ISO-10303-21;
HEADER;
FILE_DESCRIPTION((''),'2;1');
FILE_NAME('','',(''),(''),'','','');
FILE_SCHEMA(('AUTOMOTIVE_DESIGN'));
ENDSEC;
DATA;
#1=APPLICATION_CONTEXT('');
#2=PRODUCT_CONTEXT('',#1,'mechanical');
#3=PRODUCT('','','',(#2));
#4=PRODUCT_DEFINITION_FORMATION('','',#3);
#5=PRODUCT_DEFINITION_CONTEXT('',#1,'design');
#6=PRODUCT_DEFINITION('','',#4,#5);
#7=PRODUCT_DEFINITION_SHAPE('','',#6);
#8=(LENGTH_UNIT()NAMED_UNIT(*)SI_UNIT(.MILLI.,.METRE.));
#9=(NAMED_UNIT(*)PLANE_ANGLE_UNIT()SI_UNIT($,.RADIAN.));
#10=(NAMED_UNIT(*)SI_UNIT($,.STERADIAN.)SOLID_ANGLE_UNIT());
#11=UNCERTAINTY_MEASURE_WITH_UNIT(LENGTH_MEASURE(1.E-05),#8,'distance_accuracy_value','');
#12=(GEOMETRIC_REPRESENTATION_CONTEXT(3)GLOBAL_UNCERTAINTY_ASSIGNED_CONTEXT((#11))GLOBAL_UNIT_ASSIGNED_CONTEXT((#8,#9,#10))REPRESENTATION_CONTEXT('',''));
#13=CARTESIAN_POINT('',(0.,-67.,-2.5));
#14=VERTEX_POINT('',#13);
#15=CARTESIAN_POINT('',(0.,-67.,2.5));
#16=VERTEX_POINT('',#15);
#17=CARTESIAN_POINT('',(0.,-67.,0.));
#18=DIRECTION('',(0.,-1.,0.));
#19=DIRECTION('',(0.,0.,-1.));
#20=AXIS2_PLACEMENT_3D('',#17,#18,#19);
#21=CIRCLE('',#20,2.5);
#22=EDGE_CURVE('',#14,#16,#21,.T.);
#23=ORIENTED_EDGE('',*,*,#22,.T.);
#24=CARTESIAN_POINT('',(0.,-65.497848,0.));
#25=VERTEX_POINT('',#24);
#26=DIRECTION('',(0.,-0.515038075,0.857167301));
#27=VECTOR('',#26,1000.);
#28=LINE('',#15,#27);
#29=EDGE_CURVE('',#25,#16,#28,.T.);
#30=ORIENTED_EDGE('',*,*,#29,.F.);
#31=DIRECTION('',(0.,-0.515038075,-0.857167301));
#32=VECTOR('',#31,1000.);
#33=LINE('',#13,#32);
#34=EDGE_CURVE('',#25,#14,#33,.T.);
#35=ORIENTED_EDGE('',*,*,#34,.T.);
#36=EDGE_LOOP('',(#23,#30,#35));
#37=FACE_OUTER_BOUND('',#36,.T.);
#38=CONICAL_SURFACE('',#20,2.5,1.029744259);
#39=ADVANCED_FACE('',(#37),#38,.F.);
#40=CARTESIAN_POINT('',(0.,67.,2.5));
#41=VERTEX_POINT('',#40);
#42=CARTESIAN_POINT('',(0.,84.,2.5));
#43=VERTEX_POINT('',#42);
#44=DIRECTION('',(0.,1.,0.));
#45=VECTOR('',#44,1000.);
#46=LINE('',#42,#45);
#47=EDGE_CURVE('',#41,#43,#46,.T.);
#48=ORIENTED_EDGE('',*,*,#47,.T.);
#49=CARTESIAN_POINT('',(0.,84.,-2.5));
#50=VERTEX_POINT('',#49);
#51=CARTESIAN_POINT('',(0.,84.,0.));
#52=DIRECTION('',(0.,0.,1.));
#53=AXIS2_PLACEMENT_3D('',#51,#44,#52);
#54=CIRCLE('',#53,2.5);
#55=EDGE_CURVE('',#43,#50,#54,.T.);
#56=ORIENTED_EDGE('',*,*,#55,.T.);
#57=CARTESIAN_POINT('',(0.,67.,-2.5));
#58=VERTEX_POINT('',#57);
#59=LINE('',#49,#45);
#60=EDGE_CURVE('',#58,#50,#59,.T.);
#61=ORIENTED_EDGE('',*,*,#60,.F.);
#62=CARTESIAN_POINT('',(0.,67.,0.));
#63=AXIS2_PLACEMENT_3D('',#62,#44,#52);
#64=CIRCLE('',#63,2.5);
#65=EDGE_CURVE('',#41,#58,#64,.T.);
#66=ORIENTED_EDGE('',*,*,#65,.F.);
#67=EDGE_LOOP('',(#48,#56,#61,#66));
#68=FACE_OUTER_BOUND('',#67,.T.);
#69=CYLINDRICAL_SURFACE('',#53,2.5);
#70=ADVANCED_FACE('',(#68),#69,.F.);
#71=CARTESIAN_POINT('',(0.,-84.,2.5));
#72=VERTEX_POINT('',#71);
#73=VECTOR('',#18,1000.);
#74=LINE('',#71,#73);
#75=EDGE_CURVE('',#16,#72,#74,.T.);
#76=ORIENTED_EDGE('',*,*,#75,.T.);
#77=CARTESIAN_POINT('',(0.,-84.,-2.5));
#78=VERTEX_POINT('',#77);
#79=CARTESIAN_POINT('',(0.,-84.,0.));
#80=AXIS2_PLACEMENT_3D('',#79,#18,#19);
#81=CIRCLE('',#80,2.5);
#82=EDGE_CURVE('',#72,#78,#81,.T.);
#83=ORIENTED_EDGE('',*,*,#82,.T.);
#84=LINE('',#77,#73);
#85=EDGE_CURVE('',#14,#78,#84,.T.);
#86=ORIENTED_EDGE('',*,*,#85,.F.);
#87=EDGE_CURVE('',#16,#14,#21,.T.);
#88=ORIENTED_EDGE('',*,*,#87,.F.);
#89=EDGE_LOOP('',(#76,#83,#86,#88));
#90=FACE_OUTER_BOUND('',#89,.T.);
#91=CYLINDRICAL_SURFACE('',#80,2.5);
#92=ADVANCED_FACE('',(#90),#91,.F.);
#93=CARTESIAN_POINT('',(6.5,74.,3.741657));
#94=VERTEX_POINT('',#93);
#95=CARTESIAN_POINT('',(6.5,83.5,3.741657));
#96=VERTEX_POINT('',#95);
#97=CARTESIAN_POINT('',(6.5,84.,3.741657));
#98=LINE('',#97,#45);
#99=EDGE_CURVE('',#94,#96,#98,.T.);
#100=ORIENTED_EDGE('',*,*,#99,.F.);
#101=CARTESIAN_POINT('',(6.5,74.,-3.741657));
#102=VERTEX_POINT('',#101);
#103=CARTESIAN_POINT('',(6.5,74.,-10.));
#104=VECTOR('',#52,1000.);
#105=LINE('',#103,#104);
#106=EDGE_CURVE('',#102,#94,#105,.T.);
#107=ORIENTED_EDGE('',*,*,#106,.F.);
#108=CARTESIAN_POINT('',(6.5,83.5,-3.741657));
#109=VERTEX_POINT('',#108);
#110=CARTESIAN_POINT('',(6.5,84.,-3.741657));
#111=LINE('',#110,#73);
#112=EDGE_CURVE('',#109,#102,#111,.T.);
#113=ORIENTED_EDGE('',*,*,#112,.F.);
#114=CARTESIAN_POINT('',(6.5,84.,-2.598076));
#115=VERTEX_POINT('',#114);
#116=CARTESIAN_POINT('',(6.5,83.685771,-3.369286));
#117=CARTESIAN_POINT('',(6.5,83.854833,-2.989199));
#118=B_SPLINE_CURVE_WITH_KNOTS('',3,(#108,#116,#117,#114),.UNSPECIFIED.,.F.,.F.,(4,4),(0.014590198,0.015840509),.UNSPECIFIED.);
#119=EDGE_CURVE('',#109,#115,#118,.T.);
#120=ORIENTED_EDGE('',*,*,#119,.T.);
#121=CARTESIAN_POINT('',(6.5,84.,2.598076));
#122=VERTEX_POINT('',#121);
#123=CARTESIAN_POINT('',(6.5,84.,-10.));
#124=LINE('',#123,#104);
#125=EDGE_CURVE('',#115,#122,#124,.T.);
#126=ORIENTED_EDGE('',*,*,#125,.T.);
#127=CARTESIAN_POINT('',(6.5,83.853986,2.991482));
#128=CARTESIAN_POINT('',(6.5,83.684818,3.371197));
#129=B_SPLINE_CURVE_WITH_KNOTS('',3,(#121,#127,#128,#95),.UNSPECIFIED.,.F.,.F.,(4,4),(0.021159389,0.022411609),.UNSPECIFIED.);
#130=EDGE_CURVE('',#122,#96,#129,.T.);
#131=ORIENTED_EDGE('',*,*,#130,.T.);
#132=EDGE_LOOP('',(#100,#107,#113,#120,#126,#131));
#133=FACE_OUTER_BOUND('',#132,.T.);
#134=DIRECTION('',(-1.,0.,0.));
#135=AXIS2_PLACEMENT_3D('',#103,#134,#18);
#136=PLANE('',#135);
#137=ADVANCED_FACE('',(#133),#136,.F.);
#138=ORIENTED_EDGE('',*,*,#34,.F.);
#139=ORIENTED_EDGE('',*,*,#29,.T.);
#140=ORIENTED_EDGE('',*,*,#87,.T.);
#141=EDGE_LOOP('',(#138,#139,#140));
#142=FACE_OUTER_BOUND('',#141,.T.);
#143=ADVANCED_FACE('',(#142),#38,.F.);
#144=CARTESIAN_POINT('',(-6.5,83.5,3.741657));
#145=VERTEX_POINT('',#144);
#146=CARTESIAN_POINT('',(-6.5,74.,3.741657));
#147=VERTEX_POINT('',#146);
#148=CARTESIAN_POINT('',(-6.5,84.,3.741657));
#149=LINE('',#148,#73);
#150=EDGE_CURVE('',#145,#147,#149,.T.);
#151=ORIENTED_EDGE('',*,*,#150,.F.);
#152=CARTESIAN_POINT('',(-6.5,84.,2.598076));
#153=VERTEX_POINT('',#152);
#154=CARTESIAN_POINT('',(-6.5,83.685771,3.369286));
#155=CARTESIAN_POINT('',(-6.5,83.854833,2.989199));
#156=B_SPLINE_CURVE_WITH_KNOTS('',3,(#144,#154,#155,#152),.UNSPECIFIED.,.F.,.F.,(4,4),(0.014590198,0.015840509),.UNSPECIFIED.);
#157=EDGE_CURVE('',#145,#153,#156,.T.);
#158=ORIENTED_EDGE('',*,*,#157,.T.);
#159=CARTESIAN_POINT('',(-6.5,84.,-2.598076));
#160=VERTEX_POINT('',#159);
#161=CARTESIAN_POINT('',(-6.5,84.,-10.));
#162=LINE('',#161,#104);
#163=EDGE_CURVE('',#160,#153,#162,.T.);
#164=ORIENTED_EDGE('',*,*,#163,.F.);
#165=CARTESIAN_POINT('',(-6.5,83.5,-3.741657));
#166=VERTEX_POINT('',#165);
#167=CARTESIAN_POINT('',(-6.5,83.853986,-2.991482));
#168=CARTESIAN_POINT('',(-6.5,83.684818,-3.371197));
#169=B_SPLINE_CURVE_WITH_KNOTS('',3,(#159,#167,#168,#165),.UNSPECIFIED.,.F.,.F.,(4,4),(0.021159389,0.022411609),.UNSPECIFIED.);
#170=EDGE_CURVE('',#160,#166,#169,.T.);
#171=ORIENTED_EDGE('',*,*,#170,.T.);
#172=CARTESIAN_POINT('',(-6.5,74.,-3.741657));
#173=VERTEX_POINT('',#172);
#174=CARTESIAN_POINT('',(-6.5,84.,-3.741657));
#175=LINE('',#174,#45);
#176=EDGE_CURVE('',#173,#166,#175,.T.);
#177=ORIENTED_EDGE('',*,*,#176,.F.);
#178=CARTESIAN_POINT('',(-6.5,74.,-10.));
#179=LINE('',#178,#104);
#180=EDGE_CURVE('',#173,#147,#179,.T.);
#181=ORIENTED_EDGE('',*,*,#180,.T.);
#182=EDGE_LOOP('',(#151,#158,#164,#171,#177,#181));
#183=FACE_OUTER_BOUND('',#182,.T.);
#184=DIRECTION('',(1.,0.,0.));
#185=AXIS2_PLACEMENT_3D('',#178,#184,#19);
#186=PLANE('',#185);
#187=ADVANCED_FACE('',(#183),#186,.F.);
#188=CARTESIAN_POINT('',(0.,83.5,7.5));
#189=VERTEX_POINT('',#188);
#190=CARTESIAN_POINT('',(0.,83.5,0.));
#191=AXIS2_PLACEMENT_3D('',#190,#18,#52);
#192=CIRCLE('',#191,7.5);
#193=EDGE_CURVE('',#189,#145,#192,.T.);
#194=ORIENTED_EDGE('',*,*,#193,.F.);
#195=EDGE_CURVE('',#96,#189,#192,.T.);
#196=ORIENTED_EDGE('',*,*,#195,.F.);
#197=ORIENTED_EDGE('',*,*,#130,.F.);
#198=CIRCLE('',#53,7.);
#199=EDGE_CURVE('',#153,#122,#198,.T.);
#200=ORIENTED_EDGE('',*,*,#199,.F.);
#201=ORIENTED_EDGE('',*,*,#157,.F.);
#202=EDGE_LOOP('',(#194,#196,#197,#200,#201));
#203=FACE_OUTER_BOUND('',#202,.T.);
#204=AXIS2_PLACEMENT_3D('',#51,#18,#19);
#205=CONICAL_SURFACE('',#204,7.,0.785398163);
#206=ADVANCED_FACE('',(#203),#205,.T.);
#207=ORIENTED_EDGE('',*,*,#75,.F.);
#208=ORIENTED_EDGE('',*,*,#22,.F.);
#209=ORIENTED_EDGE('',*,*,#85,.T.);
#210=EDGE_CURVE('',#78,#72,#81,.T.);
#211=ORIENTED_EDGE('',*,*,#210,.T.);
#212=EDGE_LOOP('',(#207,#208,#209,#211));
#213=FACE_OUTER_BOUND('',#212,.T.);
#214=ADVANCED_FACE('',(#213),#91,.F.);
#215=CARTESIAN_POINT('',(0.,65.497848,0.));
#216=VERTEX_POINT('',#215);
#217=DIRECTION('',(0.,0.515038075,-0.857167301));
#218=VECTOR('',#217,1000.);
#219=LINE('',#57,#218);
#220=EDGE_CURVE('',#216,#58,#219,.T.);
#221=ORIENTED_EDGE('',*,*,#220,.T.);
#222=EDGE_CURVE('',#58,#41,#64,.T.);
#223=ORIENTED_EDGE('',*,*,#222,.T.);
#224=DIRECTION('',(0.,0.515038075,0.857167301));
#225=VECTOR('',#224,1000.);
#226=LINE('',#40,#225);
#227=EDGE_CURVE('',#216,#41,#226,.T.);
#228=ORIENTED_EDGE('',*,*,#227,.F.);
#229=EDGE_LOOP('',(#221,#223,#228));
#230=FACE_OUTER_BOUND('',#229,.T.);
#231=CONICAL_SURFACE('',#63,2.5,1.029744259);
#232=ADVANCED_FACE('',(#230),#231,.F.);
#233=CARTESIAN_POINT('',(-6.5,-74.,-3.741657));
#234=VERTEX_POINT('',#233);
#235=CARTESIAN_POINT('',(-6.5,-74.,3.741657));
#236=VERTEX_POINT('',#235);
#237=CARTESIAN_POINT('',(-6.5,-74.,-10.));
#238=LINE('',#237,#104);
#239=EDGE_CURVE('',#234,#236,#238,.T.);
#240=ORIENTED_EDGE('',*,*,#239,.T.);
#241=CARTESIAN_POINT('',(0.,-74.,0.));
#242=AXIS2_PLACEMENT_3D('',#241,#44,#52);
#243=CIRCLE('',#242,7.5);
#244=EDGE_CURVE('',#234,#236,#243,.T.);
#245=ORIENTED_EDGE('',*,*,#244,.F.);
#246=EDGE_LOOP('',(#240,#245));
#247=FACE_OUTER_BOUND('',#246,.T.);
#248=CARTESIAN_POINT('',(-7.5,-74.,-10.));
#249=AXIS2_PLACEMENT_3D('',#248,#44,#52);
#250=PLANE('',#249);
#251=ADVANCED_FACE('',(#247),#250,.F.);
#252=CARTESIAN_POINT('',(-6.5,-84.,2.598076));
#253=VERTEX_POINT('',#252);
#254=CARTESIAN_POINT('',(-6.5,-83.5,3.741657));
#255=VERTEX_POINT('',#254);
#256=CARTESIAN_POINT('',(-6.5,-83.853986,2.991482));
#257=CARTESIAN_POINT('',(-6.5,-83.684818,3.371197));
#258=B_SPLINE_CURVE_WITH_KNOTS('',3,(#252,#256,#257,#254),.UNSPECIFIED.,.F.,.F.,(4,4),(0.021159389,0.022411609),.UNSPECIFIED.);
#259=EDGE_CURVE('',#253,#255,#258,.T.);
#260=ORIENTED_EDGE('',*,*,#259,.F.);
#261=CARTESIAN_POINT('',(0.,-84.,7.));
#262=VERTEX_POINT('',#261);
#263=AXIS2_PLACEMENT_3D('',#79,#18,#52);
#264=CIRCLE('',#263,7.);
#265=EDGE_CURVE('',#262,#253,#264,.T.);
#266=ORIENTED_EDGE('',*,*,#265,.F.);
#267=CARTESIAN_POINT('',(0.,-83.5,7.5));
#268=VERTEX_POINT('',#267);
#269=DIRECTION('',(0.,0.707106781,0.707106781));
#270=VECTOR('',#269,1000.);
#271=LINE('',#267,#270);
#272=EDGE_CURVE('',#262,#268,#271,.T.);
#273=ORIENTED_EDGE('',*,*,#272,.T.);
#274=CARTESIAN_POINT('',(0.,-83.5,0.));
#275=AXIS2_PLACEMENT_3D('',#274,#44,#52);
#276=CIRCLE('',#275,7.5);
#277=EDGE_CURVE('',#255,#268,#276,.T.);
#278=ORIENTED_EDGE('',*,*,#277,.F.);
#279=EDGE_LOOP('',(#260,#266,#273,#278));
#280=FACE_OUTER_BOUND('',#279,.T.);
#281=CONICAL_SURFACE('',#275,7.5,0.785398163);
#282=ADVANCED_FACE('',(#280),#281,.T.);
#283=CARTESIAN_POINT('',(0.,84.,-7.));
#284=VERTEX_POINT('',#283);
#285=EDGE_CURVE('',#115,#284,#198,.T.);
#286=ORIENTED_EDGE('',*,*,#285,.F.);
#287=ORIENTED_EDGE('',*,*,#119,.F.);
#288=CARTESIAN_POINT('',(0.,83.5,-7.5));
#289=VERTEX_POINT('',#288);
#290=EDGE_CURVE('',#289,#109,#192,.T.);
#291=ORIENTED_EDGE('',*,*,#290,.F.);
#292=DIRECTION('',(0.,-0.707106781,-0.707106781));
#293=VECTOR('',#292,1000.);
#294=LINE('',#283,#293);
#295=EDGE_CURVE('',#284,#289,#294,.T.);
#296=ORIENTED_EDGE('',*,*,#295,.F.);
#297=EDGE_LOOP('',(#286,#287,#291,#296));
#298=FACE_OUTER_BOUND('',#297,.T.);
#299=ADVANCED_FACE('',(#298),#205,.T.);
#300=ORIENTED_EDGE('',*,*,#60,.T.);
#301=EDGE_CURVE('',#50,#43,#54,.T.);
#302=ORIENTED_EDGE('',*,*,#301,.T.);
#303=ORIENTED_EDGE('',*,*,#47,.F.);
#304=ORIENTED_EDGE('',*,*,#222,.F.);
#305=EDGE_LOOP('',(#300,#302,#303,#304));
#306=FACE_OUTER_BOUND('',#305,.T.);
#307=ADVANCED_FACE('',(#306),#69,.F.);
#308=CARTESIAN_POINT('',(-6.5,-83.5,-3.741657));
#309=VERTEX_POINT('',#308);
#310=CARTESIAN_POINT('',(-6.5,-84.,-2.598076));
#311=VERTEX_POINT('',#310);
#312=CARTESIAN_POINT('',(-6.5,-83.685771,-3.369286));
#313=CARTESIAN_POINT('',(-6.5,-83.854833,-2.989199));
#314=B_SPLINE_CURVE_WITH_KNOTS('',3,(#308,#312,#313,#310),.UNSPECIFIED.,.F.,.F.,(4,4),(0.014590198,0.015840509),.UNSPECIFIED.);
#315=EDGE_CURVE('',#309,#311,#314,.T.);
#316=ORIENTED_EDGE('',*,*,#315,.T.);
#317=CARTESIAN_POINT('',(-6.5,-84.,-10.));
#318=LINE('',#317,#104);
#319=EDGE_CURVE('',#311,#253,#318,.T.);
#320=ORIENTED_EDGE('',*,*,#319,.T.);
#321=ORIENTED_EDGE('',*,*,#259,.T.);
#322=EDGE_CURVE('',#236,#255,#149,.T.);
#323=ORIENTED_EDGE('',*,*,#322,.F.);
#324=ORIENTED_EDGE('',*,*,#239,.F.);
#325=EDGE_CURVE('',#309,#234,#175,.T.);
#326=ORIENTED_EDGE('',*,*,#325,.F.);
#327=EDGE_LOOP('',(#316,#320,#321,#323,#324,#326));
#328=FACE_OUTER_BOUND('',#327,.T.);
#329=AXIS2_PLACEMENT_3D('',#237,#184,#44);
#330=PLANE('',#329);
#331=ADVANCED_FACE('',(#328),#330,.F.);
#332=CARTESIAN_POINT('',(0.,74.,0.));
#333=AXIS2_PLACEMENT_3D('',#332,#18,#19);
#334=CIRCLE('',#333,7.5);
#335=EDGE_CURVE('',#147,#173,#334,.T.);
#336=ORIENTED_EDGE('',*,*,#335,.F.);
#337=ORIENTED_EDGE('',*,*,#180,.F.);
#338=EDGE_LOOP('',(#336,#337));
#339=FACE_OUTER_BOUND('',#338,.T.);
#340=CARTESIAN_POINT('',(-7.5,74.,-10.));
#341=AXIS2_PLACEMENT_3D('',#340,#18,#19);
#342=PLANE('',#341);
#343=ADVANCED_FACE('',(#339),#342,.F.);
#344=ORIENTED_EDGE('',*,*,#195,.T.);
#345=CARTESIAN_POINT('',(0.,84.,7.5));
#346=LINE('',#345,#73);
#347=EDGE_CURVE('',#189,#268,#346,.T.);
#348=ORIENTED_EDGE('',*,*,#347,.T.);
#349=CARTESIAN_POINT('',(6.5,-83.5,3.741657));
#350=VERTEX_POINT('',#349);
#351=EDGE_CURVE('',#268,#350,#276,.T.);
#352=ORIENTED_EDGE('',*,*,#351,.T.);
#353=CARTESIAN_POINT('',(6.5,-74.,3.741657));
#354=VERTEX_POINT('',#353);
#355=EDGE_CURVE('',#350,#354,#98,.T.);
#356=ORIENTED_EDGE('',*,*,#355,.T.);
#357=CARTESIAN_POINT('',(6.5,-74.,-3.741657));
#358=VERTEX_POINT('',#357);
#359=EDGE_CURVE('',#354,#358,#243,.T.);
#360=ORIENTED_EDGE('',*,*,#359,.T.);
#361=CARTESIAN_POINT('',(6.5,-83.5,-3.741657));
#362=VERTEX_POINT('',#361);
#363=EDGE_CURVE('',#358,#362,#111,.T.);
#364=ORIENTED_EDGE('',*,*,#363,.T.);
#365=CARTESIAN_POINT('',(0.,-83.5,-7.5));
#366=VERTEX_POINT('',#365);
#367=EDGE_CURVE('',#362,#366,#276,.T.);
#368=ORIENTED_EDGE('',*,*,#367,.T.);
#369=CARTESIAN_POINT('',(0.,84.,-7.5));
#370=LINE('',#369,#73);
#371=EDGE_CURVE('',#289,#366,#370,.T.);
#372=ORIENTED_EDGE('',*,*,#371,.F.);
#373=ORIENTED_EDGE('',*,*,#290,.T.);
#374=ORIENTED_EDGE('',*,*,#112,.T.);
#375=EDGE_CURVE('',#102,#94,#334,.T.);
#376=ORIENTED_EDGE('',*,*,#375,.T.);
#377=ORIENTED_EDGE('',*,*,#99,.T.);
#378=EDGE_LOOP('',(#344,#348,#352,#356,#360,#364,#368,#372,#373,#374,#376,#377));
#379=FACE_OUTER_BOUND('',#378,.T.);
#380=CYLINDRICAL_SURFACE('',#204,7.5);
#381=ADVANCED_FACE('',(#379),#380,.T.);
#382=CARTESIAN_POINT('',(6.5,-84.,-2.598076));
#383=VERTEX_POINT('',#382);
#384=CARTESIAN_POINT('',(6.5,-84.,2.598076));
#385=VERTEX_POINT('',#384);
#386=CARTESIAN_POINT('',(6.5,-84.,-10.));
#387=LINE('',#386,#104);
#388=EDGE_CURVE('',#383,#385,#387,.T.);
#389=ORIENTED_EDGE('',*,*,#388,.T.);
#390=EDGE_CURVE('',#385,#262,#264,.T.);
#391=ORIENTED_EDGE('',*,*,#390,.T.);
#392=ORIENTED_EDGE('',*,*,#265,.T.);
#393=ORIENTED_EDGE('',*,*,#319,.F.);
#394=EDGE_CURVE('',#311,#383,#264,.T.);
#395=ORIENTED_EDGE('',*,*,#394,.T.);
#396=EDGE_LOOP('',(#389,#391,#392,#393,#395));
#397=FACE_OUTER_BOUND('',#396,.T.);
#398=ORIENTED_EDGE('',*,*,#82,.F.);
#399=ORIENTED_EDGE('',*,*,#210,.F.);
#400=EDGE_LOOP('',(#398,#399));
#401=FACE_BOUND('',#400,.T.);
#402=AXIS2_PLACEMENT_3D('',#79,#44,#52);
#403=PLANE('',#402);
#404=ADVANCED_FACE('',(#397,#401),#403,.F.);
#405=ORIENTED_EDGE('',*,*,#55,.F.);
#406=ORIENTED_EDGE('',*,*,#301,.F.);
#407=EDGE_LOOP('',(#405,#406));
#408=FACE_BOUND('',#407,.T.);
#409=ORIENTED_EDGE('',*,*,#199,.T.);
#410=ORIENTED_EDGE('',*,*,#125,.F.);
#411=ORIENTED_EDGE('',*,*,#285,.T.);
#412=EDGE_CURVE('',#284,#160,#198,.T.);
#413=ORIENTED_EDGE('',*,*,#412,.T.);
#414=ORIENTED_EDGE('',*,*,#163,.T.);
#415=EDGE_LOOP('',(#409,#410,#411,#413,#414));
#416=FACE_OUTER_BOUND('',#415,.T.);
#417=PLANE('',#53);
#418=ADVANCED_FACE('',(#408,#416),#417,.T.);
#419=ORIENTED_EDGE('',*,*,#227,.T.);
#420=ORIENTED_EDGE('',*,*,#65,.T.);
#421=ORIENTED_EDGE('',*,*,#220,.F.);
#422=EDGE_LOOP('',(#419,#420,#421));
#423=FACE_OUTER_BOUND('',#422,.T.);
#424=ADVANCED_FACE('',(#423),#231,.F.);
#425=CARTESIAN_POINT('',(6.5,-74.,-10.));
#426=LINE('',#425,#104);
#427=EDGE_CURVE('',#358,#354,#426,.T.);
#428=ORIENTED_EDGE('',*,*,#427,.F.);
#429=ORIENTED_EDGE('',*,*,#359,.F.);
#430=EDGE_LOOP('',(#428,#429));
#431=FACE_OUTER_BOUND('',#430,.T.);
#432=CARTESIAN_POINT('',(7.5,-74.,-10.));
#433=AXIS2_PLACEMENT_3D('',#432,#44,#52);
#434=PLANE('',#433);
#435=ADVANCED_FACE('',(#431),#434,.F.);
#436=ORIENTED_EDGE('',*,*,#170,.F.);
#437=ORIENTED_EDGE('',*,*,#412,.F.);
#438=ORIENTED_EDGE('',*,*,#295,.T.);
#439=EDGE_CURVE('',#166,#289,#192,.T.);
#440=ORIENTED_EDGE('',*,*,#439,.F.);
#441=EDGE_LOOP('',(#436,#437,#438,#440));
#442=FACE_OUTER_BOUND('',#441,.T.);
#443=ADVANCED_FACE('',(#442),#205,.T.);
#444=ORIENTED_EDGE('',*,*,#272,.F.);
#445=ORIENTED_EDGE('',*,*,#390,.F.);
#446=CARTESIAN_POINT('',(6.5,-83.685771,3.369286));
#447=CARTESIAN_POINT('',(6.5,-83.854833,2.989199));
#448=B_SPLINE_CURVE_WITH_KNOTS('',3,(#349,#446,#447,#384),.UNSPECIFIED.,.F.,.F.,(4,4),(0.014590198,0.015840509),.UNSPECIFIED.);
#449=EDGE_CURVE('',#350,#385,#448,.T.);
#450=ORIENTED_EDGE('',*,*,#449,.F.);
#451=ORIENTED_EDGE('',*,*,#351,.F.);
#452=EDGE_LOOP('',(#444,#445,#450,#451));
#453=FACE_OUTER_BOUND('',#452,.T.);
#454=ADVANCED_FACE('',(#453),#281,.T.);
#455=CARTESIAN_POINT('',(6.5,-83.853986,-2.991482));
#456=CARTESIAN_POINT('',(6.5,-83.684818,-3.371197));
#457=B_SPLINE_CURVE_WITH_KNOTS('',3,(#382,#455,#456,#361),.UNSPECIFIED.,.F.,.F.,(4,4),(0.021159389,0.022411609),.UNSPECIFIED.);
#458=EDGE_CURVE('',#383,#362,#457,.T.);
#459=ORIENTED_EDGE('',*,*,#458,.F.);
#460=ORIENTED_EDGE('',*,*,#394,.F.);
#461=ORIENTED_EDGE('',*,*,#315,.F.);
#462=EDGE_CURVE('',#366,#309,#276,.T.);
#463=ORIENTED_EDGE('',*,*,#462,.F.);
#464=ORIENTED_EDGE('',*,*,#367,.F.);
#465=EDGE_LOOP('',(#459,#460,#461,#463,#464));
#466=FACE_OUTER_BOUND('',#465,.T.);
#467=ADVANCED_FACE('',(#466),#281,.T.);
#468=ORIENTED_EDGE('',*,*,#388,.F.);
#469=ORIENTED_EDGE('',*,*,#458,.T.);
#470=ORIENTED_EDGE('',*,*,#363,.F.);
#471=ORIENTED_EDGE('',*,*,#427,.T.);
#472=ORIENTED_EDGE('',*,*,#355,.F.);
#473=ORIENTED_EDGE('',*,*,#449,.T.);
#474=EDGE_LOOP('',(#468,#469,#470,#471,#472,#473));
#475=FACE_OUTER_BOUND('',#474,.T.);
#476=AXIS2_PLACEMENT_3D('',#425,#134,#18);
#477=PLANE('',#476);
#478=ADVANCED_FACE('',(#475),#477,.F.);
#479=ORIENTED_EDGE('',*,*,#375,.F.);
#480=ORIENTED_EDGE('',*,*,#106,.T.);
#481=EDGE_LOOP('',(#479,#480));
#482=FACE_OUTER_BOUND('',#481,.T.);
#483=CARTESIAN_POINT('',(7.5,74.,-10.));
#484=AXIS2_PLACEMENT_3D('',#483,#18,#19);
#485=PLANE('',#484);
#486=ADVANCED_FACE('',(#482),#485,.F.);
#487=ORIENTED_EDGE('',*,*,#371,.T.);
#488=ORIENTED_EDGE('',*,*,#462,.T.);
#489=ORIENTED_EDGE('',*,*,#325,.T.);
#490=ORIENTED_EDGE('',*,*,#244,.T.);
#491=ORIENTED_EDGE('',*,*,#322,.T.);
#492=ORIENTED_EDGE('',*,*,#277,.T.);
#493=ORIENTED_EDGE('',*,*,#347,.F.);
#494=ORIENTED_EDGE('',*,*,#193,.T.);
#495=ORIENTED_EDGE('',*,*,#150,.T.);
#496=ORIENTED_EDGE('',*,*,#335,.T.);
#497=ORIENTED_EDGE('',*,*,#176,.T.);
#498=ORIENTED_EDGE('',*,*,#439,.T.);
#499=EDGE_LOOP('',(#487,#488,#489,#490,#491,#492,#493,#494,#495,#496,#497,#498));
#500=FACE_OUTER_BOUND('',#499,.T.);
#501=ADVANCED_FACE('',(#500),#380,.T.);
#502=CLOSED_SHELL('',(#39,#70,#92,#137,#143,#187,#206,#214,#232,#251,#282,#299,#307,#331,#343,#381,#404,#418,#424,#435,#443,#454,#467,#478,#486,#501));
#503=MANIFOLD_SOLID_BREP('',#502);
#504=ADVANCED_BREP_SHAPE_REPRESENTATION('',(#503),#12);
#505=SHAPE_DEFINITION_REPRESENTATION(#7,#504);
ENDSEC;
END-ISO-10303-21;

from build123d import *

# Parameters (mm, degrees)
SKETCH_1_R          = 7.5
EXTRUDE_1_DEPTH     = 84
CHAMFER_1_SIZE      = 0.5
SKETCH_4_W          = 1
SKETCH_4_H          = 10
CUT_EXTRUDE_1_DEPTH = 10


with BuildPart() as part:
    # 草图1 → 凸台-拉伸1 (new, symmetric)
    with BuildSketch(Plane(origin=(0, 0, 0), x_dir=(1, 0, 0), z_dir=(0, 1, 0))):
        with Locations(Location((0, 0, 0), (0, 0, 90))):
            Circle(SKETCH_1_R)
    extrude(amount=EXTRUDE_1_DEPTH, both=True)

    # 倒角1
    chamfer_1_edges = [part.edges().sort_by_distance(p)[0] for p in [
        (0, -84, 7.5),
        (0, 84, 7.5),
    ]]
    chamfer(chamfer_1_edges, length=CHAMFER_1_SIZE)

    # 草图2 → M6 螺纹孔1 (revolve, cut)
    with BuildSketch(Plane(origin=(0, 84, 0), x_dir=(0, 0, 1), z_dir=(1, 0, 0))):
        Polygon((0, 0), (0, 18.502151548), (2.5, 17), (2.5, 0), align=None)
    hole_wizard_m6_1 = revolve(axis=Axis((0, 90.35, 0), (0, -1, 0)), mode=Mode.SUBTRACT)

    # 镜向1: M6 螺纹孔1 across plane
    add(hole_wizard_m6_1.mirror(Plane.ZX), mode=Mode.SUBTRACT)

    # 草图4 → 切除-拉伸1 (cut, symmetric)
    with BuildSketch(Plane.XY):
        with Locations((-7, 79)):
            Rectangle(SKETCH_4_W, SKETCH_4_H)
        with Locations((7, 79)):
            Rectangle(SKETCH_4_W, SKETCH_4_H)
        with Locations((7, -79)):
            Rectangle(SKETCH_4_W, SKETCH_4_H)
        with Locations((-7, -79)):
            Rectangle(SKETCH_4_W, SKETCH_4_H)
    extrude(amount=CUT_EXTRUDE_1_DEPTH, both=True, mode=Mode.SUBTRACT)


solid = part.part
